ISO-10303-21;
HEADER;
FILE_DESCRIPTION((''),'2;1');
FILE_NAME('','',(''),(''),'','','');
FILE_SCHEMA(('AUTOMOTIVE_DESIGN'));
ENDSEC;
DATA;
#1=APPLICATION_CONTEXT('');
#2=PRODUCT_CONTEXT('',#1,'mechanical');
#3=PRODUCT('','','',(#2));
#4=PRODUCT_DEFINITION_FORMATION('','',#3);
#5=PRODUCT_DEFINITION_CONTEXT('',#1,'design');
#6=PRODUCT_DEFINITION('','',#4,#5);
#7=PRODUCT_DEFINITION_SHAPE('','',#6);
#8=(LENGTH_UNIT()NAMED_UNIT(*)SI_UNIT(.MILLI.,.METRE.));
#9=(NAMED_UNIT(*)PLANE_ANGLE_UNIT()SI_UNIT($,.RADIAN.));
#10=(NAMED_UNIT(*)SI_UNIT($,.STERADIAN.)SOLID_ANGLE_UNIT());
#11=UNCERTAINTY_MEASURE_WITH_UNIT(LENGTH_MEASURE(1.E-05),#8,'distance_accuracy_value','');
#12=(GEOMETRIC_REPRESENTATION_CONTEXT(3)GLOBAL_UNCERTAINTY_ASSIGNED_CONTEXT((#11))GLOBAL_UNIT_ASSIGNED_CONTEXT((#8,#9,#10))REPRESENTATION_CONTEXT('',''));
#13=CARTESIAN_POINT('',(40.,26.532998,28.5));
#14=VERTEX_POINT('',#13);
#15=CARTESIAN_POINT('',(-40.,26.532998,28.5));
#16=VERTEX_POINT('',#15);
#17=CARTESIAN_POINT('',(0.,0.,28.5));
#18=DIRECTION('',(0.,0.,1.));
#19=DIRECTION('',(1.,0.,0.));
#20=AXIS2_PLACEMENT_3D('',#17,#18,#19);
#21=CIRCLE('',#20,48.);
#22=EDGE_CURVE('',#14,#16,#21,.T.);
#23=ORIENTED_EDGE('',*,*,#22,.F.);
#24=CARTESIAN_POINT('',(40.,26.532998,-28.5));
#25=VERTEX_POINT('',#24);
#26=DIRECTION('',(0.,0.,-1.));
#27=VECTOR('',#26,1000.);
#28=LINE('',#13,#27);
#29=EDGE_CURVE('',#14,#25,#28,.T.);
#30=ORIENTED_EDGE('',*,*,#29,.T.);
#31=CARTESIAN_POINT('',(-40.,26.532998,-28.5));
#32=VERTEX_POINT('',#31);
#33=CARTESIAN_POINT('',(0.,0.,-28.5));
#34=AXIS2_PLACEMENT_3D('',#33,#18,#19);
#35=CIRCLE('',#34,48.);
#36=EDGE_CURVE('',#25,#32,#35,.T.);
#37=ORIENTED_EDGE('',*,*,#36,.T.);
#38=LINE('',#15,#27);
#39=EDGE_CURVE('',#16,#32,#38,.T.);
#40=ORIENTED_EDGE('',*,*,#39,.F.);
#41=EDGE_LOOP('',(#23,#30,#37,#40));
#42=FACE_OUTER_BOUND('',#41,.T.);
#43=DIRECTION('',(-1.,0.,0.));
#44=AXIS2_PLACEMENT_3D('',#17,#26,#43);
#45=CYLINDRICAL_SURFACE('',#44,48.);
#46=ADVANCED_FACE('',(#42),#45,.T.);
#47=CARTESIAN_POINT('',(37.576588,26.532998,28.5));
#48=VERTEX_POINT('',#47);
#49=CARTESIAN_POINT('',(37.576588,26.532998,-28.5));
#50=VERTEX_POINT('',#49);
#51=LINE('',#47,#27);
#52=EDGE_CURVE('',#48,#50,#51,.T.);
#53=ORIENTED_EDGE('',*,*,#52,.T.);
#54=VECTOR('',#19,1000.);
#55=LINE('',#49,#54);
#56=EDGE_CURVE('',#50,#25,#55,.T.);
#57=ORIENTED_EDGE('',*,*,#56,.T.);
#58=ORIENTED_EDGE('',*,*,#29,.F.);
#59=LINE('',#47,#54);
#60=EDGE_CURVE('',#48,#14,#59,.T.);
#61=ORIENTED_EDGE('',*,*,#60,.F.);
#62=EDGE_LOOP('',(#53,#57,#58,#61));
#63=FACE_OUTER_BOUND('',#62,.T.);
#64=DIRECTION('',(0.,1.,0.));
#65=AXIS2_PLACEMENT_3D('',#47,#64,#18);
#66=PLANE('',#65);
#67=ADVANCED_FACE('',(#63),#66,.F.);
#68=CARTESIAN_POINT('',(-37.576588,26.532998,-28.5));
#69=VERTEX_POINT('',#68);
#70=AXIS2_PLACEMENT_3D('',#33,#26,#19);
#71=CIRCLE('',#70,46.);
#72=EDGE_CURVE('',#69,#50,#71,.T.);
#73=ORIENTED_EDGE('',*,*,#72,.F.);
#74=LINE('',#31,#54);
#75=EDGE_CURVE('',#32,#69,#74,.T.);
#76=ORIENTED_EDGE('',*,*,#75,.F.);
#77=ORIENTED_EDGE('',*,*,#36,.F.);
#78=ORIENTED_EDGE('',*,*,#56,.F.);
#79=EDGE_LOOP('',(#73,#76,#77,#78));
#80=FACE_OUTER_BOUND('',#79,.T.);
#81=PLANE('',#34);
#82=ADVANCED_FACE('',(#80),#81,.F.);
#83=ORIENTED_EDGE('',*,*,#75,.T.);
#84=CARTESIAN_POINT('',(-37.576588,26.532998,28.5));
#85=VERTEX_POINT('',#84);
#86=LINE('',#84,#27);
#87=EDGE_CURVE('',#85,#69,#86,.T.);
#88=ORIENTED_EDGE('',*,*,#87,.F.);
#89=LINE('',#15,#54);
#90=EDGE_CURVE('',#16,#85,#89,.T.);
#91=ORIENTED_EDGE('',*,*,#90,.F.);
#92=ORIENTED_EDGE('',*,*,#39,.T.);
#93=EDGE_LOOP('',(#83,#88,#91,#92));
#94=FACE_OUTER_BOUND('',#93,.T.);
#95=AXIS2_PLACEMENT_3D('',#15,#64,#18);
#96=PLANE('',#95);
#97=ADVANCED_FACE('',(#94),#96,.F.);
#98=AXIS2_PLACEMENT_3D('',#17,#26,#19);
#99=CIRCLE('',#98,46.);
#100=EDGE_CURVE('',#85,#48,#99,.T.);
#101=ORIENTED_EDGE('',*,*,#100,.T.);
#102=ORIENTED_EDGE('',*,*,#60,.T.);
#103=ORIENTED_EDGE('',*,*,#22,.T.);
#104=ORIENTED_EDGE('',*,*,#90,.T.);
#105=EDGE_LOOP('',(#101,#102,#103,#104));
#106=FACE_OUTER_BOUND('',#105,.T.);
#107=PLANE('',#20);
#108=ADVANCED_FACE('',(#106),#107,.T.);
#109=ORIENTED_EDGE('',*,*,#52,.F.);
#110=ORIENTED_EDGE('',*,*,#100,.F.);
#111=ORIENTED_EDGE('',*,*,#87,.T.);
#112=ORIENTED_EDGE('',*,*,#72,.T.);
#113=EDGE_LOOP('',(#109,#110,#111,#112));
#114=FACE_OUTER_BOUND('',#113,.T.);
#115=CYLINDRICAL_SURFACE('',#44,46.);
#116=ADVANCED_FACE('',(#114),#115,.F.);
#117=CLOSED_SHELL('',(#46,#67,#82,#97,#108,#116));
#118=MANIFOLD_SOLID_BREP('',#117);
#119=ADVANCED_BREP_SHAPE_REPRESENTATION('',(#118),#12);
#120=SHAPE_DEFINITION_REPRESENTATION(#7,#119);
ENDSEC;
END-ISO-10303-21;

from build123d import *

# Parameters (mm, degrees)
BOSS_EXTRUDE1_DEPTH = 28.5


with BuildPart() as part:
    # Sketch1 → Boss-Extrude1 (new, symmetric)
    with BuildSketch(Plane.XY):
        with BuildLine():
            Line((-40, 26.532998323), (-37.576588456, 26.532998323))
            ThreePointArc((-37.576588456, 26.532998323), (0, 46), (37.576588456, 26.532998323))
            Line((37.576588456, 26.532998323), (40, 26.532998323))
            ThreePointArc((40, 26.532998323), (0, 48), (-40, 26.532998323))
        make_face()
    extrude(amount=BOSS_EXTRUDE1_DEPTH, both=True)


solid = part.part
